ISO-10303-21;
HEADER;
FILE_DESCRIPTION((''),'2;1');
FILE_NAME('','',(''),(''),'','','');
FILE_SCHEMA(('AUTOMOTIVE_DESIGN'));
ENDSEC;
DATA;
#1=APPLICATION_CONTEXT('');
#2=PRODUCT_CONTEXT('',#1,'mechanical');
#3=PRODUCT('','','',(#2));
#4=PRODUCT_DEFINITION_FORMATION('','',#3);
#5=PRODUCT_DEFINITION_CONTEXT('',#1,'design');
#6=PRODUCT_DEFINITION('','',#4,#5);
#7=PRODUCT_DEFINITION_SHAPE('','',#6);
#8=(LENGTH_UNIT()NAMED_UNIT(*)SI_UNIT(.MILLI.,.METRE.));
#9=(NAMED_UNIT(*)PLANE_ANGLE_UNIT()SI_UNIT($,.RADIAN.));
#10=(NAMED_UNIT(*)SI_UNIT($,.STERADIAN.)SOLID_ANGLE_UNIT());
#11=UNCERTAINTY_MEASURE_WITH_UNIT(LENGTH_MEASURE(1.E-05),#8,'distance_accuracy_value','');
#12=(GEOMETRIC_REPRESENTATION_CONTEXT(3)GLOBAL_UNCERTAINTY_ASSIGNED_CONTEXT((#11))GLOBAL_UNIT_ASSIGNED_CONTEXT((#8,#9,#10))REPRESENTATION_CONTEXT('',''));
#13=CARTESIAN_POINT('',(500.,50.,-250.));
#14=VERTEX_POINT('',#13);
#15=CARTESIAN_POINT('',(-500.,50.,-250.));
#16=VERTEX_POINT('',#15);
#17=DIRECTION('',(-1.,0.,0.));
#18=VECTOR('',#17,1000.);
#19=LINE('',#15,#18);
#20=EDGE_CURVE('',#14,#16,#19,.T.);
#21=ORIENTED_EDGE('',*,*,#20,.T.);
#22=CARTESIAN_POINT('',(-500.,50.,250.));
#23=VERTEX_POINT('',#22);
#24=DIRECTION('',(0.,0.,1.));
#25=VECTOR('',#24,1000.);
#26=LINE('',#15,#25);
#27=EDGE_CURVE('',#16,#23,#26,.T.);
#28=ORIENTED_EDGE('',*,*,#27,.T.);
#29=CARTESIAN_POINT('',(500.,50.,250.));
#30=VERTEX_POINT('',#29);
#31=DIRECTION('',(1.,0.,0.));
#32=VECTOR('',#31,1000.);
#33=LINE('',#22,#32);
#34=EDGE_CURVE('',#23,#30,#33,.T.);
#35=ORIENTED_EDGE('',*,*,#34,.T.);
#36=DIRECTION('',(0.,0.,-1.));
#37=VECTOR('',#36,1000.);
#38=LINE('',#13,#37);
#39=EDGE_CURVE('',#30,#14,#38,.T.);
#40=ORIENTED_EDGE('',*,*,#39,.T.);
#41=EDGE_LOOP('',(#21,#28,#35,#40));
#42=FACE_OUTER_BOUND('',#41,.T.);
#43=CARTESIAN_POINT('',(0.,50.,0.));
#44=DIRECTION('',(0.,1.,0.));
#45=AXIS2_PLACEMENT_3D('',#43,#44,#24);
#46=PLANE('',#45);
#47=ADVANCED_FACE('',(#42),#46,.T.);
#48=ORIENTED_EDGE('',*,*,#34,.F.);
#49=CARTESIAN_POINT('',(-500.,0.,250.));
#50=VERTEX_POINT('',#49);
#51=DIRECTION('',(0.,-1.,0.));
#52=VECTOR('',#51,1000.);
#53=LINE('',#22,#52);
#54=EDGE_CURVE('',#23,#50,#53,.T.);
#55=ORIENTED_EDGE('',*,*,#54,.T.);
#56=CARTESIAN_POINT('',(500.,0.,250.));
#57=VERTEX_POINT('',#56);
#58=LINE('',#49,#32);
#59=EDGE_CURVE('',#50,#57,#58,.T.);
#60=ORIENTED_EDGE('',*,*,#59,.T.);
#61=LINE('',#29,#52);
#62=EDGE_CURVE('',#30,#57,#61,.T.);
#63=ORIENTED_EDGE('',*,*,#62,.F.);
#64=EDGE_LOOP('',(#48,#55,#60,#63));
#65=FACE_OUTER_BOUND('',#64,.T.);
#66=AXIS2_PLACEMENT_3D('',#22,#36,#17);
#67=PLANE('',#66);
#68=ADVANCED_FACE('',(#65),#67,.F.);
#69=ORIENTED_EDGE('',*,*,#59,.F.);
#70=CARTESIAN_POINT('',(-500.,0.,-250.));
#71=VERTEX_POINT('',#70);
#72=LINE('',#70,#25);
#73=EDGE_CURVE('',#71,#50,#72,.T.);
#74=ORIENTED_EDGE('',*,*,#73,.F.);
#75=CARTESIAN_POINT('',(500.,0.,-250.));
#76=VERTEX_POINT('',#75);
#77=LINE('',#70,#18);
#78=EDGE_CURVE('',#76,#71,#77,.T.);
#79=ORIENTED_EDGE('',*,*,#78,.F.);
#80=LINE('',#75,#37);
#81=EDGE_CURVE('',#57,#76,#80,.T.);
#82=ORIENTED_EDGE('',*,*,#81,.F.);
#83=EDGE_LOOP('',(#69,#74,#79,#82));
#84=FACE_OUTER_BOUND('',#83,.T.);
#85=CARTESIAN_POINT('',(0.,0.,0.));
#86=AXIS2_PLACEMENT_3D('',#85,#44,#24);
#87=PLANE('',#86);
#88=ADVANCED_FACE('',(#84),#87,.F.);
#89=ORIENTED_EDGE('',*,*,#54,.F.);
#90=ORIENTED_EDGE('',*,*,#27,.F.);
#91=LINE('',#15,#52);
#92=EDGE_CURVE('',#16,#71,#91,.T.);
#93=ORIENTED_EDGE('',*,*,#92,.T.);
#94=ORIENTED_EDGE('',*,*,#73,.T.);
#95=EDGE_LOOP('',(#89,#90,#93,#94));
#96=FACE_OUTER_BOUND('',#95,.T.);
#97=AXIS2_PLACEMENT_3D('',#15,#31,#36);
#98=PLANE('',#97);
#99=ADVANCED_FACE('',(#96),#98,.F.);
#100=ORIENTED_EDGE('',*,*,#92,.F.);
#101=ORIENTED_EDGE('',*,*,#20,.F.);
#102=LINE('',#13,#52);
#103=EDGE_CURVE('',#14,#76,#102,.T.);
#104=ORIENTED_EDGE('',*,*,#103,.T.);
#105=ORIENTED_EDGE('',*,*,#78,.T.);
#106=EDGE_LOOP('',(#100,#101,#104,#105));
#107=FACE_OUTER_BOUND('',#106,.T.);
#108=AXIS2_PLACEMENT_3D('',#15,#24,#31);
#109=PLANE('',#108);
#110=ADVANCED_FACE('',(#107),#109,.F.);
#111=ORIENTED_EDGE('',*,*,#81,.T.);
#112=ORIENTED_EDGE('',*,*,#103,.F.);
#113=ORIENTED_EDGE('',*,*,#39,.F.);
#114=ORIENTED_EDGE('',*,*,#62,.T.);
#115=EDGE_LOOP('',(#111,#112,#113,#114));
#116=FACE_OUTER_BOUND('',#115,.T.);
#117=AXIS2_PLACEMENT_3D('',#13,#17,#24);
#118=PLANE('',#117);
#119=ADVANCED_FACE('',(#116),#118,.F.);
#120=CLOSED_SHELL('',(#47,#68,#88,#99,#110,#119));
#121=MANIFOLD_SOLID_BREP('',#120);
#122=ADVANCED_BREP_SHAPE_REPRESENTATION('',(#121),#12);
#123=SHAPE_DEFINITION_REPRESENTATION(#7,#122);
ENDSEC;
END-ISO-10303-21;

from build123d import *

# Parameters (mm, degrees)
SKETCH_1_W      = 1000
SKETCH_1_H      = 500
EXTRUDE_1_DEPTH = 50


with BuildPart() as part:
    # 草图1 → 凸台-拉伸1 (new body)
    with BuildSketch(Plane(origin=(0, 0, 0), x_dir=(1, 0, 0), z_dir=(0, 1, 0))):
        Rectangle(SKETCH_1_W, SKETCH_1_H)
    extrude(amount=EXTRUDE_1_DEPTH)


solid = part.part
